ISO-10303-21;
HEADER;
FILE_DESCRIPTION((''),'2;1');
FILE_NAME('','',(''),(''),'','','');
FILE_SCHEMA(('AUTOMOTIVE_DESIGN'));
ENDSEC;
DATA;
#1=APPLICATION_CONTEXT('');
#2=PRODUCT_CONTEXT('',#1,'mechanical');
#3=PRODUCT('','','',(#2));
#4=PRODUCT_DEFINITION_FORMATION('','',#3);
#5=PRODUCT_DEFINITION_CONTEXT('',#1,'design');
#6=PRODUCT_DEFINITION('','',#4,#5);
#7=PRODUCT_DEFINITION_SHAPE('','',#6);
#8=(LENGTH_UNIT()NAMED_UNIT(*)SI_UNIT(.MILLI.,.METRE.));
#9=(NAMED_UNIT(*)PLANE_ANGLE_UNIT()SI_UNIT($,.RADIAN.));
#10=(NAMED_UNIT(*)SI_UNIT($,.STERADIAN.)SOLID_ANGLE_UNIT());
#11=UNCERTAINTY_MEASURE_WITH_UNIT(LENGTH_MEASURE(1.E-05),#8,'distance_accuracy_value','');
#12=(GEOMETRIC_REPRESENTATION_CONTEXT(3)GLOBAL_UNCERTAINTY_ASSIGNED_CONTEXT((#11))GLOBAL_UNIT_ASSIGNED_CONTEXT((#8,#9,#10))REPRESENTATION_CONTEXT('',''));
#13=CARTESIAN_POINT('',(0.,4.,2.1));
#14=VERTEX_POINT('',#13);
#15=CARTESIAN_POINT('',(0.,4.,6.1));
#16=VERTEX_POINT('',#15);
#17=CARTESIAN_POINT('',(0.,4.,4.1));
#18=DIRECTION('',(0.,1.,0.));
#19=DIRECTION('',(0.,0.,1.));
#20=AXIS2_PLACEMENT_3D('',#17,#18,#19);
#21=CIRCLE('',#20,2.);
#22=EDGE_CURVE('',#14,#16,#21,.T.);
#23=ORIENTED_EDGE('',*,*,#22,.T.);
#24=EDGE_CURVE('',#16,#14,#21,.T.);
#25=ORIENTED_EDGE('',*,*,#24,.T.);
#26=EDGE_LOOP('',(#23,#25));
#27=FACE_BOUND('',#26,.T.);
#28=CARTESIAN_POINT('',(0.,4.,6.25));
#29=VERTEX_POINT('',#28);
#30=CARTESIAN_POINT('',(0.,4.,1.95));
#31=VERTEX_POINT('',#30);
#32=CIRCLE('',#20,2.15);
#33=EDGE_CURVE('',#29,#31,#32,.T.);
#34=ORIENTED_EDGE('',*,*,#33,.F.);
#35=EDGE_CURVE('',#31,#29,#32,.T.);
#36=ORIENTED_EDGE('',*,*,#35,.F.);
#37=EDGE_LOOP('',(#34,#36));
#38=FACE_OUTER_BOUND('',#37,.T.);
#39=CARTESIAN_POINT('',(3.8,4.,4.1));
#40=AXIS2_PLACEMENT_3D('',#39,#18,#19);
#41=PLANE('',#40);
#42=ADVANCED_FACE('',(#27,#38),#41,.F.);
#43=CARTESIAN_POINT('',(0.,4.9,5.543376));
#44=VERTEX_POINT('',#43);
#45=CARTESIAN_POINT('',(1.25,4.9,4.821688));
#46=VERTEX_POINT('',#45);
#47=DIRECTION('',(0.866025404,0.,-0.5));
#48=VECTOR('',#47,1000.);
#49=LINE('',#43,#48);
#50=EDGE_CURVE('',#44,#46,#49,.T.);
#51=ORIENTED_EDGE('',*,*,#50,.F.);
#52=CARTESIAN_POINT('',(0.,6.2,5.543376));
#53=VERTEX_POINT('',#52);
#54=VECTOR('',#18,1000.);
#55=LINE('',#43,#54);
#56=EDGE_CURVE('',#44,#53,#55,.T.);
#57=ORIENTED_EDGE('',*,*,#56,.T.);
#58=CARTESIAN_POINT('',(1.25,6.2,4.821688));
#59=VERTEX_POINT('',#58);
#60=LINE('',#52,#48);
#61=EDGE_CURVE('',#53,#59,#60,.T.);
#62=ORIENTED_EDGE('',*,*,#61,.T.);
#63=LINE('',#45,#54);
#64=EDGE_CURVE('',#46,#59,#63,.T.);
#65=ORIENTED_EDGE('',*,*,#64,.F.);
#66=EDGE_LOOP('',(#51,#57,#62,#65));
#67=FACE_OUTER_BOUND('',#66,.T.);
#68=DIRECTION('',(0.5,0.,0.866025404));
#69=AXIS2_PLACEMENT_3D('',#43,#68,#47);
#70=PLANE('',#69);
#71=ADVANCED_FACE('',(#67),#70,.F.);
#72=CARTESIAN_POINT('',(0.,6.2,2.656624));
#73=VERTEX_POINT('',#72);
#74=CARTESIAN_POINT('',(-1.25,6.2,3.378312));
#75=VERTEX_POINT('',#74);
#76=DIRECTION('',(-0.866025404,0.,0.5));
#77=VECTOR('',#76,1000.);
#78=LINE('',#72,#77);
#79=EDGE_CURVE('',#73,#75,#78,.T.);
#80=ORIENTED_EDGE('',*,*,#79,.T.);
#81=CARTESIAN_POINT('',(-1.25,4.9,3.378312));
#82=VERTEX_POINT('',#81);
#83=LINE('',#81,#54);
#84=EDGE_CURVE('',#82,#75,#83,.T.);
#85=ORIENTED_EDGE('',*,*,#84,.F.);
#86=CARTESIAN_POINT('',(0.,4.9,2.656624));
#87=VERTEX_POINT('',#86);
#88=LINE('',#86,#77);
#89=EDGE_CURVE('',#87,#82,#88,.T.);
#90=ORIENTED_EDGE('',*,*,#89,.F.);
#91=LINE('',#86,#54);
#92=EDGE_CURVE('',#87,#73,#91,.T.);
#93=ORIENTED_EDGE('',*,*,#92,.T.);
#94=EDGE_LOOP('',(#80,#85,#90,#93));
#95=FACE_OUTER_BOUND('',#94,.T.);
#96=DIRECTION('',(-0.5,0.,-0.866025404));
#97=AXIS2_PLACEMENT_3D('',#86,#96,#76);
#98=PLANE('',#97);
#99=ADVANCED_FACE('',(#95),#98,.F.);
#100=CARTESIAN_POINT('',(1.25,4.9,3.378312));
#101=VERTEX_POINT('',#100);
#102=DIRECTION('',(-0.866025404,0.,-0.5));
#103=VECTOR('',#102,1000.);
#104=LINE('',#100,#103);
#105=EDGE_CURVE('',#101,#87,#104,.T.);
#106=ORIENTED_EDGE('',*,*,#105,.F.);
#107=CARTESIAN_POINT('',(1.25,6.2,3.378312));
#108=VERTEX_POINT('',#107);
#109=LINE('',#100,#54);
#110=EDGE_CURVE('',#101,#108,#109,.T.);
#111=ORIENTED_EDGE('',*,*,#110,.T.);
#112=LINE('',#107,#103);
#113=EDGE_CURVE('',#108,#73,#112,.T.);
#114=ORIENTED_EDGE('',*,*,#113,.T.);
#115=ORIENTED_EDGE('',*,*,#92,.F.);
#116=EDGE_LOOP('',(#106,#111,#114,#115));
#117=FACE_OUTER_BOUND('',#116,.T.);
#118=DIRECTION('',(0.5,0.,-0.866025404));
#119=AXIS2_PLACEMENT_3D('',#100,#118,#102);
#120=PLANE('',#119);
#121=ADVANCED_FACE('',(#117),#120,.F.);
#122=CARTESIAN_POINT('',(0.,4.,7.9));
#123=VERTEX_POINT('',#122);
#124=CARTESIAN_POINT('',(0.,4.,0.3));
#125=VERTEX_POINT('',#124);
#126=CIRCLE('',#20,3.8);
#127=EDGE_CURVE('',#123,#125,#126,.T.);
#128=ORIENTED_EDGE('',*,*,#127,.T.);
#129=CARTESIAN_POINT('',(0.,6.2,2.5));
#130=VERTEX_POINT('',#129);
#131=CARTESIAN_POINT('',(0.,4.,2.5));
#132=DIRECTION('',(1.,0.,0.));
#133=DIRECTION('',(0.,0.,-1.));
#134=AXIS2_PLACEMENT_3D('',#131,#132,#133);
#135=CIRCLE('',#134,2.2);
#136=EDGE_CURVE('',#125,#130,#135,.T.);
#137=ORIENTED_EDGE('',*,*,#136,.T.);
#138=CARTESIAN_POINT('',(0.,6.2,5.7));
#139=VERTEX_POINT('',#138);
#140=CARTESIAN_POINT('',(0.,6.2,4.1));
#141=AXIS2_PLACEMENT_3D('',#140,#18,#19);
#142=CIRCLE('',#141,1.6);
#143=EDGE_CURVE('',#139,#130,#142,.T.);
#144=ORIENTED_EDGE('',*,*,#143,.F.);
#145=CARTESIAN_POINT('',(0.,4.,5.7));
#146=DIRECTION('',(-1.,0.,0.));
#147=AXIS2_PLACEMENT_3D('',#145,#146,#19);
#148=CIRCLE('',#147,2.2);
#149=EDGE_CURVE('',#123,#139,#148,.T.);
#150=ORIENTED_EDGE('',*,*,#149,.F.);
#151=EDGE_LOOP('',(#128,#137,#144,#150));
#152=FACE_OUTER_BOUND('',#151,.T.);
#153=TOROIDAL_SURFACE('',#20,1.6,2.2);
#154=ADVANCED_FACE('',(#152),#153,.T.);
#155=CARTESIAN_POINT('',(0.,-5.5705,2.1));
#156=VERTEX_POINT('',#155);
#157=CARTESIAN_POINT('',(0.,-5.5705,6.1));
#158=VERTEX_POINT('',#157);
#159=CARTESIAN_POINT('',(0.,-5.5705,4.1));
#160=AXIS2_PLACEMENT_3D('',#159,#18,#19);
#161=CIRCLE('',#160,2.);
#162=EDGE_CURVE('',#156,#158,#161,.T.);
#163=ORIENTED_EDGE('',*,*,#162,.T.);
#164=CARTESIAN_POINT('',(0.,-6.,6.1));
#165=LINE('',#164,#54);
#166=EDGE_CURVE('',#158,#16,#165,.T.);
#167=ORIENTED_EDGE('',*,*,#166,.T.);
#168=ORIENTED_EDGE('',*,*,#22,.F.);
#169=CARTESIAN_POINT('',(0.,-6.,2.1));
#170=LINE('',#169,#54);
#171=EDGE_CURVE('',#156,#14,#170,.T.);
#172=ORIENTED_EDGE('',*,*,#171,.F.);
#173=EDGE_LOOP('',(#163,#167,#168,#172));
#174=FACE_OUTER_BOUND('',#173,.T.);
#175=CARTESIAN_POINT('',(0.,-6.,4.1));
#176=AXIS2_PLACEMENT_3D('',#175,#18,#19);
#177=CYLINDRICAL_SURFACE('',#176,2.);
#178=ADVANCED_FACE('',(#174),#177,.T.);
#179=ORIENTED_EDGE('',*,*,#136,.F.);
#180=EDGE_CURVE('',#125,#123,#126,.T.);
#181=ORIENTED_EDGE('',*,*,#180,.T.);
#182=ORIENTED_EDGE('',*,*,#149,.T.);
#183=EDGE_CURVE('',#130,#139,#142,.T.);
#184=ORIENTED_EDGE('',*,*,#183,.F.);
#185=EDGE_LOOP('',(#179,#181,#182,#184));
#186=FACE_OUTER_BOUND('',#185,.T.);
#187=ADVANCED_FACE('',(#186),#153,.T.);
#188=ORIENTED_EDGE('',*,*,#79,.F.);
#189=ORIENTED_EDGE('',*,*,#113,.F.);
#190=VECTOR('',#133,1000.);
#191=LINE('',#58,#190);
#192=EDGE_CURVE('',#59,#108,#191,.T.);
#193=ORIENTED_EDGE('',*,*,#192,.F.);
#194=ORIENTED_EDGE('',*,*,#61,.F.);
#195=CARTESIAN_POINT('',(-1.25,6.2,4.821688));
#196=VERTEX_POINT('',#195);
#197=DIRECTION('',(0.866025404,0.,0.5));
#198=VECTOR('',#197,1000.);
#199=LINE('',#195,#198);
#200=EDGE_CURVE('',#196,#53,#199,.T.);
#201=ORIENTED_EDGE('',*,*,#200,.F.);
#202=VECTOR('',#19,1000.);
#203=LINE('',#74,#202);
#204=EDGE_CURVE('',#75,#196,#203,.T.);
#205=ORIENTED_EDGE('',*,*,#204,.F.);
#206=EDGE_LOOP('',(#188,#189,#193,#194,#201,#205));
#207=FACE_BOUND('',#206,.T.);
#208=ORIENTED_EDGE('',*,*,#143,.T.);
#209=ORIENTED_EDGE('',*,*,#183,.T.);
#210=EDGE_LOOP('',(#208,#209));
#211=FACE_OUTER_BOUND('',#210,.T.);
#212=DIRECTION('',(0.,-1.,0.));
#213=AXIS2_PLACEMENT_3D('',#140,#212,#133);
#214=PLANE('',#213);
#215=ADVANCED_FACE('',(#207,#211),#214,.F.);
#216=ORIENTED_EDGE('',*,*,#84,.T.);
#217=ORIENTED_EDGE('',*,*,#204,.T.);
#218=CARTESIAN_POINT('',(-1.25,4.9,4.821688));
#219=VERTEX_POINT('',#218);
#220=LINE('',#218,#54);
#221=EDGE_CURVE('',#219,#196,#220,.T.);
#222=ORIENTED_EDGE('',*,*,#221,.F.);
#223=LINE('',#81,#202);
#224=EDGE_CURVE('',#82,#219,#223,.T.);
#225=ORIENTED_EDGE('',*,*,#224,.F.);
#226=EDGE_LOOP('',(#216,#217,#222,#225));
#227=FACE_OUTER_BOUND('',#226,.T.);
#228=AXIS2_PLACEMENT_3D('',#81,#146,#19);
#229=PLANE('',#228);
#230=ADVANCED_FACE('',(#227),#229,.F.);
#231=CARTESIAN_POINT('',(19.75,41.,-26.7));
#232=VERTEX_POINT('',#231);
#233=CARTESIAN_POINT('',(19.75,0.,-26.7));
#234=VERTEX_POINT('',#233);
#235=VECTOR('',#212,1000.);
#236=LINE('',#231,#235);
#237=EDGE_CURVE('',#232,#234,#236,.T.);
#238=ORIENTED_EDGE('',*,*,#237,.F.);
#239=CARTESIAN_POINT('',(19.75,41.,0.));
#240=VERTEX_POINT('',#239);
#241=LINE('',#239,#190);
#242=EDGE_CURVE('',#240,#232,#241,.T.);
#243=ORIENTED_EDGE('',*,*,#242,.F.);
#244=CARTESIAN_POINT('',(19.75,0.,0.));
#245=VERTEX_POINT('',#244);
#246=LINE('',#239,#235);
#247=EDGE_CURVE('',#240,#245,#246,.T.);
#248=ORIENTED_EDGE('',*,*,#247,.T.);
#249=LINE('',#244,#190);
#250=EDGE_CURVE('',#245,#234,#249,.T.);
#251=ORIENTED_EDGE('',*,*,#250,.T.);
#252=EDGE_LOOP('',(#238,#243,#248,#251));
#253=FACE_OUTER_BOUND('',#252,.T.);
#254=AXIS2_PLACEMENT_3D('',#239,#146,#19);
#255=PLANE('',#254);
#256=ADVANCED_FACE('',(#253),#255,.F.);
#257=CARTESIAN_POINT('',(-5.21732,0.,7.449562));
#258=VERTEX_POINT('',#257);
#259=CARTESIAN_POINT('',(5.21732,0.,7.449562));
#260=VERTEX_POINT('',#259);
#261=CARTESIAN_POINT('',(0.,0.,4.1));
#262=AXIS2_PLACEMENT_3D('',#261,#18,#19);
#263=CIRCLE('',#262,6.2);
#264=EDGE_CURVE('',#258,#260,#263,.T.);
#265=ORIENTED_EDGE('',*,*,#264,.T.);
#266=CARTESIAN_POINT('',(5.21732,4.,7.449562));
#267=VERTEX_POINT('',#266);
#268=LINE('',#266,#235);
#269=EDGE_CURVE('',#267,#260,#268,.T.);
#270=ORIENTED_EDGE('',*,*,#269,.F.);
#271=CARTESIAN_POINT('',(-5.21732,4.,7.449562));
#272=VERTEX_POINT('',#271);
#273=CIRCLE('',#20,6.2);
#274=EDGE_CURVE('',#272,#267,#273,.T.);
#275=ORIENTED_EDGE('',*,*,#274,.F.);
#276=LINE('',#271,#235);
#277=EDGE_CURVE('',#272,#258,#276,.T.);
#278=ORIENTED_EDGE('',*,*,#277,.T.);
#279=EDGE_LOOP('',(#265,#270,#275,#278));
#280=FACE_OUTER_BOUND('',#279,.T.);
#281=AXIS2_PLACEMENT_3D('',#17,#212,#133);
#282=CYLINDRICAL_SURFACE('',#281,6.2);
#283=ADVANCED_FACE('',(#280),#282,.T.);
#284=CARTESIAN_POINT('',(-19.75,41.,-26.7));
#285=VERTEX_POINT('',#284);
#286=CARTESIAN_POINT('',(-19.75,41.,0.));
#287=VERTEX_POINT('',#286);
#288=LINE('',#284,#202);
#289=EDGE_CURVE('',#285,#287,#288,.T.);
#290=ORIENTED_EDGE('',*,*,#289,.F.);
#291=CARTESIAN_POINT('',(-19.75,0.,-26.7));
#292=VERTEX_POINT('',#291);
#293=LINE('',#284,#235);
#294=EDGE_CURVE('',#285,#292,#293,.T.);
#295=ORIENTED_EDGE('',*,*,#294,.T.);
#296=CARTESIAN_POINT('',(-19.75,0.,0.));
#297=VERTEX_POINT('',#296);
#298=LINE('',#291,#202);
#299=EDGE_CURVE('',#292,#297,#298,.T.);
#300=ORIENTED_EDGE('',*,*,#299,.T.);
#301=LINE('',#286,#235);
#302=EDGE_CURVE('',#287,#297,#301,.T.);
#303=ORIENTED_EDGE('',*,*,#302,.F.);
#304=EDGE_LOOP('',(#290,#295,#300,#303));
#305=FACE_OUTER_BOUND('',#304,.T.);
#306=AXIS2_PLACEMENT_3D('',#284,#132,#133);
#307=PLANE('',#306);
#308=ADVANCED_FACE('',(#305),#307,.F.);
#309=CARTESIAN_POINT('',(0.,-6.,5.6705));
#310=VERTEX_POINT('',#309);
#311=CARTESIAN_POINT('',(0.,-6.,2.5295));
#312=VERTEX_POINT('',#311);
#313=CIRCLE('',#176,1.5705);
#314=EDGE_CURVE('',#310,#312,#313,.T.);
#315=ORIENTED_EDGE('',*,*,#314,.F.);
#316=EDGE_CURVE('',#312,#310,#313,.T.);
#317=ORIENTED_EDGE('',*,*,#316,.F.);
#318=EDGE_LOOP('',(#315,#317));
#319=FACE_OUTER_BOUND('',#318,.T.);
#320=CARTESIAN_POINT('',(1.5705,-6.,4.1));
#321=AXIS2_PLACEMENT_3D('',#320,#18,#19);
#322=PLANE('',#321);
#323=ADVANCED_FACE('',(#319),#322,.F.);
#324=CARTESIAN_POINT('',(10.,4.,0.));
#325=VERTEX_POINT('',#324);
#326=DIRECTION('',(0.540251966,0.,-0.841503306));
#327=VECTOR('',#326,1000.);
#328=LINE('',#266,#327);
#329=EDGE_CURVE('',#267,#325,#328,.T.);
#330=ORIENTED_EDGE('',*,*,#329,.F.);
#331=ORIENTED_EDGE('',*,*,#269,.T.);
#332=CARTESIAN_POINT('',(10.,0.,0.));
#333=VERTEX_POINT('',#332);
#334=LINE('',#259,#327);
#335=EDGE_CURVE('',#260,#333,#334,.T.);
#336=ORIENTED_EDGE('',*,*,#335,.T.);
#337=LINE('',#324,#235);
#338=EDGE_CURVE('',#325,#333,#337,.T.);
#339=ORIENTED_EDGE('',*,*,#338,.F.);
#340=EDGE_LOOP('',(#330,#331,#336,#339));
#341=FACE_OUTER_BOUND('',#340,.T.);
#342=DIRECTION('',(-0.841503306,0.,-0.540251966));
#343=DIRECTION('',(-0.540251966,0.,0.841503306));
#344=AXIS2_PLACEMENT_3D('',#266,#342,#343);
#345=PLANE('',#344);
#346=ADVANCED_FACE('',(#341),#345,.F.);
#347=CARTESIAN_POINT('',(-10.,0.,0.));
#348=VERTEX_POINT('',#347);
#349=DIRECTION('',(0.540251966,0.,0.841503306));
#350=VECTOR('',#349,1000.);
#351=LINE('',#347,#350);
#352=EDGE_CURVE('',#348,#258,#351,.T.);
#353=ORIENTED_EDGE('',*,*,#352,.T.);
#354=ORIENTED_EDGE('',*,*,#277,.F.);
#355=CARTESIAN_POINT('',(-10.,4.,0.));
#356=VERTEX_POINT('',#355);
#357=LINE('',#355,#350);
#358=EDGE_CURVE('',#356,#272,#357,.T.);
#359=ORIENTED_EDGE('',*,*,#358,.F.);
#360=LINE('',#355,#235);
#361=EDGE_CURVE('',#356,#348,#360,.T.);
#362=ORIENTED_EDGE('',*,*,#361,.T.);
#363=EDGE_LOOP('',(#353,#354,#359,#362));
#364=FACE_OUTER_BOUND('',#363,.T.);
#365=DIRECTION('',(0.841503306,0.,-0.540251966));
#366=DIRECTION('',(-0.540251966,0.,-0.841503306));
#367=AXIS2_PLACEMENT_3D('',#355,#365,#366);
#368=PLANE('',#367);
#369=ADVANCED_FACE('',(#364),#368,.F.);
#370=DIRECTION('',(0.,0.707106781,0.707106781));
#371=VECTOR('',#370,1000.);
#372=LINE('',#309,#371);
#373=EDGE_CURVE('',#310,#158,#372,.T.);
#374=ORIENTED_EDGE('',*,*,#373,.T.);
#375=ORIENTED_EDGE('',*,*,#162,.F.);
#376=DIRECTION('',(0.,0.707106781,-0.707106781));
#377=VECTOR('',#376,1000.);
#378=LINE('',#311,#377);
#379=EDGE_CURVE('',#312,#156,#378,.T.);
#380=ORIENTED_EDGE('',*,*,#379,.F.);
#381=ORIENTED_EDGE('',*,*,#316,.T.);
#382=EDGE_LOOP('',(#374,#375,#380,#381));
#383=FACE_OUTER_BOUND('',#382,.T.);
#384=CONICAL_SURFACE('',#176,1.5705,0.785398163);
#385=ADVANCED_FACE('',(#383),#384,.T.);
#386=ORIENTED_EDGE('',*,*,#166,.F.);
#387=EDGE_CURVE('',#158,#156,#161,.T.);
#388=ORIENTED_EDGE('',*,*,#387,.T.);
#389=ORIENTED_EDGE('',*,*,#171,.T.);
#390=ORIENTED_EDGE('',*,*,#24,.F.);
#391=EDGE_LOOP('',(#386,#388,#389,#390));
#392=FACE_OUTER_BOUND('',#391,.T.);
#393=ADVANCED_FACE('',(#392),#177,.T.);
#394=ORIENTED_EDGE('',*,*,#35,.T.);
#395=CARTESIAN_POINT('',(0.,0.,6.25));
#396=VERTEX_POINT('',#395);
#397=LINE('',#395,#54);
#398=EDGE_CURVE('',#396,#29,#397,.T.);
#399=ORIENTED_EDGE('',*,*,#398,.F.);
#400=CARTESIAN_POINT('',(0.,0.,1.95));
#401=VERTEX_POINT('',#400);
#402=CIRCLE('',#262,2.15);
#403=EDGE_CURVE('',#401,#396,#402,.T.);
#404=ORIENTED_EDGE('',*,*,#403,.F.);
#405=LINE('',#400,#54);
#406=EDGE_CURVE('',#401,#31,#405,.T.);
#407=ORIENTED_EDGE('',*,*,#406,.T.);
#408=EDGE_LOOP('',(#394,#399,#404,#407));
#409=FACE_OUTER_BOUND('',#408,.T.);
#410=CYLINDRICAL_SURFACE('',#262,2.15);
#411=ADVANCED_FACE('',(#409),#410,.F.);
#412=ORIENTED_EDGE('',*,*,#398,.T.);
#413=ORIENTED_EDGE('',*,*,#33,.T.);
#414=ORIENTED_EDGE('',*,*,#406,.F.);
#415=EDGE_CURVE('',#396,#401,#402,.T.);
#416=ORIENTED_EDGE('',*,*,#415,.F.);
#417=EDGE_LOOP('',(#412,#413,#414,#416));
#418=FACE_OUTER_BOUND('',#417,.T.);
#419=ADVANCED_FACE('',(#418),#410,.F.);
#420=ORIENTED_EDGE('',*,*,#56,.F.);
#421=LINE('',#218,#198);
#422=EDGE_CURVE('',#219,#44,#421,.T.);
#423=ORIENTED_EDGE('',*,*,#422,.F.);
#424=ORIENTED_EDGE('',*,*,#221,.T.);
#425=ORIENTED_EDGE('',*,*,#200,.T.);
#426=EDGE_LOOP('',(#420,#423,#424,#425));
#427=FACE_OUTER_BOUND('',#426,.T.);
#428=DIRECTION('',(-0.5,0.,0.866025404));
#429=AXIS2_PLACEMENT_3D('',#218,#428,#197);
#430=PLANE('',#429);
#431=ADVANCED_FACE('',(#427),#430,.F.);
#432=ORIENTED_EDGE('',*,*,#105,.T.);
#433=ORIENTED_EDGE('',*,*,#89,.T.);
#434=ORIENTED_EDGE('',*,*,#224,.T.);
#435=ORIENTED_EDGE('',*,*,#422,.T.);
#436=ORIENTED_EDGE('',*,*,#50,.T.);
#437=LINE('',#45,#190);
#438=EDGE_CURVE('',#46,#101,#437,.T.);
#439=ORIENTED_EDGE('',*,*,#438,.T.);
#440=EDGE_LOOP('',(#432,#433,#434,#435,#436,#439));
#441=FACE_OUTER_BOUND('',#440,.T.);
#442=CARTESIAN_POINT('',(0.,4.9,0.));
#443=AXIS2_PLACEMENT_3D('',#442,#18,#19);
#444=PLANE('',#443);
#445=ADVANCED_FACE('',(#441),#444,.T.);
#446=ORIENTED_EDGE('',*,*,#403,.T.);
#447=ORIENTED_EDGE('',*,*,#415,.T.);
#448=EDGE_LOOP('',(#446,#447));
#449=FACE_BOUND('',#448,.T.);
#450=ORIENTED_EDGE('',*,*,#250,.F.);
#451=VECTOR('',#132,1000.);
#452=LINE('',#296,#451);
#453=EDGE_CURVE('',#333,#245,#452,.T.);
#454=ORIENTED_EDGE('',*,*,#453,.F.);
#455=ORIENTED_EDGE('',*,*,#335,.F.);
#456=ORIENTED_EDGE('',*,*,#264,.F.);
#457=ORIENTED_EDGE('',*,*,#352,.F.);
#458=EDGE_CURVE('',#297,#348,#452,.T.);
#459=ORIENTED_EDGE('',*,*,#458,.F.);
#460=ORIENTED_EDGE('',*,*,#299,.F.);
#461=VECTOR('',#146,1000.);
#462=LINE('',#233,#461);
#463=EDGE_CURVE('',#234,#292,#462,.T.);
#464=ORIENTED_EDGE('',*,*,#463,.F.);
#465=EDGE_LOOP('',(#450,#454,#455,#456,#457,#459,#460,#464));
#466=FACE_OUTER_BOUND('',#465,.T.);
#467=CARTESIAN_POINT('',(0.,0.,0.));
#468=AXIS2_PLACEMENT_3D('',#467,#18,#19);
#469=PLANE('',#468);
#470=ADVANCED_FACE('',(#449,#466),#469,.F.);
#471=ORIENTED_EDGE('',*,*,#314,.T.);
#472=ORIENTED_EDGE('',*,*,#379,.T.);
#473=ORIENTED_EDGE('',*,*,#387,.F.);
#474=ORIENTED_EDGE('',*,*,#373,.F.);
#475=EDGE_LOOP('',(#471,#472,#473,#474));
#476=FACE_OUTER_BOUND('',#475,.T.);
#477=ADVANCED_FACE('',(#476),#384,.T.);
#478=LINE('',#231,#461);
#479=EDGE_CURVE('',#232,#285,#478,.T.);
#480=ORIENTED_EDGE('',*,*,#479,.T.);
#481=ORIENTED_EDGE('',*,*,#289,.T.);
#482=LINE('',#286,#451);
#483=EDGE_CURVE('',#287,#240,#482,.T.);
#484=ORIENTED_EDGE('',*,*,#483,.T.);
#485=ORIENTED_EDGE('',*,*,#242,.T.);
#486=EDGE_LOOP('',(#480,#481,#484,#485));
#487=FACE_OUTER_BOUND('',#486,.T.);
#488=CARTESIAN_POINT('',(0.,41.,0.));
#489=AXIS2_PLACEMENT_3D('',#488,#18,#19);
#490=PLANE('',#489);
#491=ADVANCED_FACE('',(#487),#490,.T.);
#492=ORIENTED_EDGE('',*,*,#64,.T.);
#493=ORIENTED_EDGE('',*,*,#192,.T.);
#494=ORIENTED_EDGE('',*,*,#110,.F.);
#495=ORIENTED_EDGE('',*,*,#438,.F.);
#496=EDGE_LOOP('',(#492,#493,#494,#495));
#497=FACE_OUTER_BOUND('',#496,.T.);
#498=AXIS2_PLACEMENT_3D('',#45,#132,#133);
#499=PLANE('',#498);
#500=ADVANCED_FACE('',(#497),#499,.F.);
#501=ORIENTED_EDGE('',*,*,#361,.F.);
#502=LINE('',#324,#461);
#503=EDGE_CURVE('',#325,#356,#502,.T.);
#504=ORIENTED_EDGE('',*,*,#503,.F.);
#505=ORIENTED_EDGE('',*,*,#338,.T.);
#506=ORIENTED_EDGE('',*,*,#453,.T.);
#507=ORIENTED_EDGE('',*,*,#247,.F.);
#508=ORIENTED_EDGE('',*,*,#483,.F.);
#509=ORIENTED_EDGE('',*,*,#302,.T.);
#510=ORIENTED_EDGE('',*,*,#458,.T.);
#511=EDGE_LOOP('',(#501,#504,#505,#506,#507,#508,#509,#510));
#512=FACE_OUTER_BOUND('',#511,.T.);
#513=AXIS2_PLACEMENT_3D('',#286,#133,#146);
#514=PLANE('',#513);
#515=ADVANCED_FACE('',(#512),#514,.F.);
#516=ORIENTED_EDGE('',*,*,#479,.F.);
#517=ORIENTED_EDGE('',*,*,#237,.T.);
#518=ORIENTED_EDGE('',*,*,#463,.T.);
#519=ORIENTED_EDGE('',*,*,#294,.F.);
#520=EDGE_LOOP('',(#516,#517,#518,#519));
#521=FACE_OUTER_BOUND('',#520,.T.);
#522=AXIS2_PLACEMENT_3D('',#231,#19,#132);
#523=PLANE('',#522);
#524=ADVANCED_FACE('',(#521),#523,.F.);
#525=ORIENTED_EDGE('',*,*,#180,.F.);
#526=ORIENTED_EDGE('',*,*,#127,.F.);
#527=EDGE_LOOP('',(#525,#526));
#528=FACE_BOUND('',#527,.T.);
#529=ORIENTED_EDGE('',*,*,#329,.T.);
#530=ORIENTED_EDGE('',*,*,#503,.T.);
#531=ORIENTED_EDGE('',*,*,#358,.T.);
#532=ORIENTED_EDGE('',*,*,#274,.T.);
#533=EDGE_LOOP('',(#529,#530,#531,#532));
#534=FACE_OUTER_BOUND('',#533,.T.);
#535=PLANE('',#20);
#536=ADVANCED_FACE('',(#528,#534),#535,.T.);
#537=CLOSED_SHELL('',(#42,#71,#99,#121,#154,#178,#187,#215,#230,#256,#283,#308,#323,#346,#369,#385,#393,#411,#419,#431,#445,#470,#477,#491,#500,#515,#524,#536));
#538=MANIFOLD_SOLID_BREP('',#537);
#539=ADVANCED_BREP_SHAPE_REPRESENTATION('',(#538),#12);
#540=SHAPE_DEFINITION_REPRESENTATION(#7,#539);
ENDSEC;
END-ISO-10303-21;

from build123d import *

# Parameters (mm, degrees)
SKETCH_1_W          = 39.5
SKETCH_1_H          = 26.7
EXTRUDE_1_DEPTH     = 41
EXTRUDE_2_DEPTH     = 4
SKETCH_3_W          = 2.15
SKETCH_3_H          = 4
CUT_EXTRUDE_1_DEPTH = 1.3


with BuildPart() as part:
    # 草图1 → 凸台-拉伸1 (new body)
    with BuildSketch(Plane(origin=(0, 0, 0), x_dir=(1, 0, 0), z_dir=(0, 1, 0))):
        with Locations((0, 13.35)):
            Rectangle(SKETCH_1_W, SKETCH_1_H)
    extrude(amount=EXTRUDE_1_DEPTH)

    # 草图2 → 凸台-拉伸2 (add)
    with BuildSketch(Plane(origin=(0, 0, 0), x_dir=(1, 0, 0), z_dir=(0, 1, 0))):
        with BuildLine():
            Line((-10, 0), (-5.217320496, -7.449562186))
            ThreePointArc((-5.217320496, -7.449562186), (0, -10.3), (5.217320496, -7.449562186))
            Line((5.217320496, -7.449562186), (10, 0))
            Line((10, 0), (-10, 0))
        make_face()
    extrude(amount=EXTRUDE_2_DEPTH)

    # 草图3 → 切除-旋转1 (revolve, cut)
    with BuildSketch(Plane.XY.offset(4.1), mode=Mode.PRIVATE) as cut_revolve_1_sk:
        with Locations((1.075, 2)):
            Rectangle(SKETCH_3_W, SKETCH_3_H)
    revolve(cut_revolve_1_sk.sketch.rotate(Axis((0, 0, 4.1), (0, 1, 0)), 270), axis=Axis((0, 0, 4.1), (0, 1, 0)), mode=Mode.SUBTRACT)

    # 草图4 → 旋转1 (revolve)
    with BuildSketch(Plane.XY.offset(4.1), mode=Mode.PRIVATE) as revolve_1_sk:
        with BuildLine():
            Line((0, 6.2), (1.6, 6.2))
            ThreePointArc((1.6, 6.2), (3.155634919, 5.555634919), (3.8, 4))
            Line((3.8, 4), (2, 4))
            Line((2, 4), (2, -5.5705))
            Line((2, -5.5705), (1.5705, -6))
            Line((1.5705, -6), (0, -6))
            Line((0, -6), (0, 6.2))
        make_face()
    revolve(revolve_1_sk.sketch.rotate(Axis((0, -6, 4.1), (0, 1, 0)), 270), axis=Axis((0, -6, 4.1), (0, 1, 0)))

    # 草图5 → 切除-拉伸1 (cut)
    with BuildSketch(Plane(origin=(0, 6.2, 0), x_dir=(1, 0, 0), z_dir=(0, 1, 0))):
        Polygon((-1.25, -3.378312164), (-1.25, -4.821687836), (0, -5.543375673), (1.25, -4.821687836), (1.25, -3.378312164), (0, -2.656624327), align=None)
    extrude(amount=-CUT_EXTRUDE_1_DEPTH, mode=Mode.SUBTRACT)


solid = part.part
